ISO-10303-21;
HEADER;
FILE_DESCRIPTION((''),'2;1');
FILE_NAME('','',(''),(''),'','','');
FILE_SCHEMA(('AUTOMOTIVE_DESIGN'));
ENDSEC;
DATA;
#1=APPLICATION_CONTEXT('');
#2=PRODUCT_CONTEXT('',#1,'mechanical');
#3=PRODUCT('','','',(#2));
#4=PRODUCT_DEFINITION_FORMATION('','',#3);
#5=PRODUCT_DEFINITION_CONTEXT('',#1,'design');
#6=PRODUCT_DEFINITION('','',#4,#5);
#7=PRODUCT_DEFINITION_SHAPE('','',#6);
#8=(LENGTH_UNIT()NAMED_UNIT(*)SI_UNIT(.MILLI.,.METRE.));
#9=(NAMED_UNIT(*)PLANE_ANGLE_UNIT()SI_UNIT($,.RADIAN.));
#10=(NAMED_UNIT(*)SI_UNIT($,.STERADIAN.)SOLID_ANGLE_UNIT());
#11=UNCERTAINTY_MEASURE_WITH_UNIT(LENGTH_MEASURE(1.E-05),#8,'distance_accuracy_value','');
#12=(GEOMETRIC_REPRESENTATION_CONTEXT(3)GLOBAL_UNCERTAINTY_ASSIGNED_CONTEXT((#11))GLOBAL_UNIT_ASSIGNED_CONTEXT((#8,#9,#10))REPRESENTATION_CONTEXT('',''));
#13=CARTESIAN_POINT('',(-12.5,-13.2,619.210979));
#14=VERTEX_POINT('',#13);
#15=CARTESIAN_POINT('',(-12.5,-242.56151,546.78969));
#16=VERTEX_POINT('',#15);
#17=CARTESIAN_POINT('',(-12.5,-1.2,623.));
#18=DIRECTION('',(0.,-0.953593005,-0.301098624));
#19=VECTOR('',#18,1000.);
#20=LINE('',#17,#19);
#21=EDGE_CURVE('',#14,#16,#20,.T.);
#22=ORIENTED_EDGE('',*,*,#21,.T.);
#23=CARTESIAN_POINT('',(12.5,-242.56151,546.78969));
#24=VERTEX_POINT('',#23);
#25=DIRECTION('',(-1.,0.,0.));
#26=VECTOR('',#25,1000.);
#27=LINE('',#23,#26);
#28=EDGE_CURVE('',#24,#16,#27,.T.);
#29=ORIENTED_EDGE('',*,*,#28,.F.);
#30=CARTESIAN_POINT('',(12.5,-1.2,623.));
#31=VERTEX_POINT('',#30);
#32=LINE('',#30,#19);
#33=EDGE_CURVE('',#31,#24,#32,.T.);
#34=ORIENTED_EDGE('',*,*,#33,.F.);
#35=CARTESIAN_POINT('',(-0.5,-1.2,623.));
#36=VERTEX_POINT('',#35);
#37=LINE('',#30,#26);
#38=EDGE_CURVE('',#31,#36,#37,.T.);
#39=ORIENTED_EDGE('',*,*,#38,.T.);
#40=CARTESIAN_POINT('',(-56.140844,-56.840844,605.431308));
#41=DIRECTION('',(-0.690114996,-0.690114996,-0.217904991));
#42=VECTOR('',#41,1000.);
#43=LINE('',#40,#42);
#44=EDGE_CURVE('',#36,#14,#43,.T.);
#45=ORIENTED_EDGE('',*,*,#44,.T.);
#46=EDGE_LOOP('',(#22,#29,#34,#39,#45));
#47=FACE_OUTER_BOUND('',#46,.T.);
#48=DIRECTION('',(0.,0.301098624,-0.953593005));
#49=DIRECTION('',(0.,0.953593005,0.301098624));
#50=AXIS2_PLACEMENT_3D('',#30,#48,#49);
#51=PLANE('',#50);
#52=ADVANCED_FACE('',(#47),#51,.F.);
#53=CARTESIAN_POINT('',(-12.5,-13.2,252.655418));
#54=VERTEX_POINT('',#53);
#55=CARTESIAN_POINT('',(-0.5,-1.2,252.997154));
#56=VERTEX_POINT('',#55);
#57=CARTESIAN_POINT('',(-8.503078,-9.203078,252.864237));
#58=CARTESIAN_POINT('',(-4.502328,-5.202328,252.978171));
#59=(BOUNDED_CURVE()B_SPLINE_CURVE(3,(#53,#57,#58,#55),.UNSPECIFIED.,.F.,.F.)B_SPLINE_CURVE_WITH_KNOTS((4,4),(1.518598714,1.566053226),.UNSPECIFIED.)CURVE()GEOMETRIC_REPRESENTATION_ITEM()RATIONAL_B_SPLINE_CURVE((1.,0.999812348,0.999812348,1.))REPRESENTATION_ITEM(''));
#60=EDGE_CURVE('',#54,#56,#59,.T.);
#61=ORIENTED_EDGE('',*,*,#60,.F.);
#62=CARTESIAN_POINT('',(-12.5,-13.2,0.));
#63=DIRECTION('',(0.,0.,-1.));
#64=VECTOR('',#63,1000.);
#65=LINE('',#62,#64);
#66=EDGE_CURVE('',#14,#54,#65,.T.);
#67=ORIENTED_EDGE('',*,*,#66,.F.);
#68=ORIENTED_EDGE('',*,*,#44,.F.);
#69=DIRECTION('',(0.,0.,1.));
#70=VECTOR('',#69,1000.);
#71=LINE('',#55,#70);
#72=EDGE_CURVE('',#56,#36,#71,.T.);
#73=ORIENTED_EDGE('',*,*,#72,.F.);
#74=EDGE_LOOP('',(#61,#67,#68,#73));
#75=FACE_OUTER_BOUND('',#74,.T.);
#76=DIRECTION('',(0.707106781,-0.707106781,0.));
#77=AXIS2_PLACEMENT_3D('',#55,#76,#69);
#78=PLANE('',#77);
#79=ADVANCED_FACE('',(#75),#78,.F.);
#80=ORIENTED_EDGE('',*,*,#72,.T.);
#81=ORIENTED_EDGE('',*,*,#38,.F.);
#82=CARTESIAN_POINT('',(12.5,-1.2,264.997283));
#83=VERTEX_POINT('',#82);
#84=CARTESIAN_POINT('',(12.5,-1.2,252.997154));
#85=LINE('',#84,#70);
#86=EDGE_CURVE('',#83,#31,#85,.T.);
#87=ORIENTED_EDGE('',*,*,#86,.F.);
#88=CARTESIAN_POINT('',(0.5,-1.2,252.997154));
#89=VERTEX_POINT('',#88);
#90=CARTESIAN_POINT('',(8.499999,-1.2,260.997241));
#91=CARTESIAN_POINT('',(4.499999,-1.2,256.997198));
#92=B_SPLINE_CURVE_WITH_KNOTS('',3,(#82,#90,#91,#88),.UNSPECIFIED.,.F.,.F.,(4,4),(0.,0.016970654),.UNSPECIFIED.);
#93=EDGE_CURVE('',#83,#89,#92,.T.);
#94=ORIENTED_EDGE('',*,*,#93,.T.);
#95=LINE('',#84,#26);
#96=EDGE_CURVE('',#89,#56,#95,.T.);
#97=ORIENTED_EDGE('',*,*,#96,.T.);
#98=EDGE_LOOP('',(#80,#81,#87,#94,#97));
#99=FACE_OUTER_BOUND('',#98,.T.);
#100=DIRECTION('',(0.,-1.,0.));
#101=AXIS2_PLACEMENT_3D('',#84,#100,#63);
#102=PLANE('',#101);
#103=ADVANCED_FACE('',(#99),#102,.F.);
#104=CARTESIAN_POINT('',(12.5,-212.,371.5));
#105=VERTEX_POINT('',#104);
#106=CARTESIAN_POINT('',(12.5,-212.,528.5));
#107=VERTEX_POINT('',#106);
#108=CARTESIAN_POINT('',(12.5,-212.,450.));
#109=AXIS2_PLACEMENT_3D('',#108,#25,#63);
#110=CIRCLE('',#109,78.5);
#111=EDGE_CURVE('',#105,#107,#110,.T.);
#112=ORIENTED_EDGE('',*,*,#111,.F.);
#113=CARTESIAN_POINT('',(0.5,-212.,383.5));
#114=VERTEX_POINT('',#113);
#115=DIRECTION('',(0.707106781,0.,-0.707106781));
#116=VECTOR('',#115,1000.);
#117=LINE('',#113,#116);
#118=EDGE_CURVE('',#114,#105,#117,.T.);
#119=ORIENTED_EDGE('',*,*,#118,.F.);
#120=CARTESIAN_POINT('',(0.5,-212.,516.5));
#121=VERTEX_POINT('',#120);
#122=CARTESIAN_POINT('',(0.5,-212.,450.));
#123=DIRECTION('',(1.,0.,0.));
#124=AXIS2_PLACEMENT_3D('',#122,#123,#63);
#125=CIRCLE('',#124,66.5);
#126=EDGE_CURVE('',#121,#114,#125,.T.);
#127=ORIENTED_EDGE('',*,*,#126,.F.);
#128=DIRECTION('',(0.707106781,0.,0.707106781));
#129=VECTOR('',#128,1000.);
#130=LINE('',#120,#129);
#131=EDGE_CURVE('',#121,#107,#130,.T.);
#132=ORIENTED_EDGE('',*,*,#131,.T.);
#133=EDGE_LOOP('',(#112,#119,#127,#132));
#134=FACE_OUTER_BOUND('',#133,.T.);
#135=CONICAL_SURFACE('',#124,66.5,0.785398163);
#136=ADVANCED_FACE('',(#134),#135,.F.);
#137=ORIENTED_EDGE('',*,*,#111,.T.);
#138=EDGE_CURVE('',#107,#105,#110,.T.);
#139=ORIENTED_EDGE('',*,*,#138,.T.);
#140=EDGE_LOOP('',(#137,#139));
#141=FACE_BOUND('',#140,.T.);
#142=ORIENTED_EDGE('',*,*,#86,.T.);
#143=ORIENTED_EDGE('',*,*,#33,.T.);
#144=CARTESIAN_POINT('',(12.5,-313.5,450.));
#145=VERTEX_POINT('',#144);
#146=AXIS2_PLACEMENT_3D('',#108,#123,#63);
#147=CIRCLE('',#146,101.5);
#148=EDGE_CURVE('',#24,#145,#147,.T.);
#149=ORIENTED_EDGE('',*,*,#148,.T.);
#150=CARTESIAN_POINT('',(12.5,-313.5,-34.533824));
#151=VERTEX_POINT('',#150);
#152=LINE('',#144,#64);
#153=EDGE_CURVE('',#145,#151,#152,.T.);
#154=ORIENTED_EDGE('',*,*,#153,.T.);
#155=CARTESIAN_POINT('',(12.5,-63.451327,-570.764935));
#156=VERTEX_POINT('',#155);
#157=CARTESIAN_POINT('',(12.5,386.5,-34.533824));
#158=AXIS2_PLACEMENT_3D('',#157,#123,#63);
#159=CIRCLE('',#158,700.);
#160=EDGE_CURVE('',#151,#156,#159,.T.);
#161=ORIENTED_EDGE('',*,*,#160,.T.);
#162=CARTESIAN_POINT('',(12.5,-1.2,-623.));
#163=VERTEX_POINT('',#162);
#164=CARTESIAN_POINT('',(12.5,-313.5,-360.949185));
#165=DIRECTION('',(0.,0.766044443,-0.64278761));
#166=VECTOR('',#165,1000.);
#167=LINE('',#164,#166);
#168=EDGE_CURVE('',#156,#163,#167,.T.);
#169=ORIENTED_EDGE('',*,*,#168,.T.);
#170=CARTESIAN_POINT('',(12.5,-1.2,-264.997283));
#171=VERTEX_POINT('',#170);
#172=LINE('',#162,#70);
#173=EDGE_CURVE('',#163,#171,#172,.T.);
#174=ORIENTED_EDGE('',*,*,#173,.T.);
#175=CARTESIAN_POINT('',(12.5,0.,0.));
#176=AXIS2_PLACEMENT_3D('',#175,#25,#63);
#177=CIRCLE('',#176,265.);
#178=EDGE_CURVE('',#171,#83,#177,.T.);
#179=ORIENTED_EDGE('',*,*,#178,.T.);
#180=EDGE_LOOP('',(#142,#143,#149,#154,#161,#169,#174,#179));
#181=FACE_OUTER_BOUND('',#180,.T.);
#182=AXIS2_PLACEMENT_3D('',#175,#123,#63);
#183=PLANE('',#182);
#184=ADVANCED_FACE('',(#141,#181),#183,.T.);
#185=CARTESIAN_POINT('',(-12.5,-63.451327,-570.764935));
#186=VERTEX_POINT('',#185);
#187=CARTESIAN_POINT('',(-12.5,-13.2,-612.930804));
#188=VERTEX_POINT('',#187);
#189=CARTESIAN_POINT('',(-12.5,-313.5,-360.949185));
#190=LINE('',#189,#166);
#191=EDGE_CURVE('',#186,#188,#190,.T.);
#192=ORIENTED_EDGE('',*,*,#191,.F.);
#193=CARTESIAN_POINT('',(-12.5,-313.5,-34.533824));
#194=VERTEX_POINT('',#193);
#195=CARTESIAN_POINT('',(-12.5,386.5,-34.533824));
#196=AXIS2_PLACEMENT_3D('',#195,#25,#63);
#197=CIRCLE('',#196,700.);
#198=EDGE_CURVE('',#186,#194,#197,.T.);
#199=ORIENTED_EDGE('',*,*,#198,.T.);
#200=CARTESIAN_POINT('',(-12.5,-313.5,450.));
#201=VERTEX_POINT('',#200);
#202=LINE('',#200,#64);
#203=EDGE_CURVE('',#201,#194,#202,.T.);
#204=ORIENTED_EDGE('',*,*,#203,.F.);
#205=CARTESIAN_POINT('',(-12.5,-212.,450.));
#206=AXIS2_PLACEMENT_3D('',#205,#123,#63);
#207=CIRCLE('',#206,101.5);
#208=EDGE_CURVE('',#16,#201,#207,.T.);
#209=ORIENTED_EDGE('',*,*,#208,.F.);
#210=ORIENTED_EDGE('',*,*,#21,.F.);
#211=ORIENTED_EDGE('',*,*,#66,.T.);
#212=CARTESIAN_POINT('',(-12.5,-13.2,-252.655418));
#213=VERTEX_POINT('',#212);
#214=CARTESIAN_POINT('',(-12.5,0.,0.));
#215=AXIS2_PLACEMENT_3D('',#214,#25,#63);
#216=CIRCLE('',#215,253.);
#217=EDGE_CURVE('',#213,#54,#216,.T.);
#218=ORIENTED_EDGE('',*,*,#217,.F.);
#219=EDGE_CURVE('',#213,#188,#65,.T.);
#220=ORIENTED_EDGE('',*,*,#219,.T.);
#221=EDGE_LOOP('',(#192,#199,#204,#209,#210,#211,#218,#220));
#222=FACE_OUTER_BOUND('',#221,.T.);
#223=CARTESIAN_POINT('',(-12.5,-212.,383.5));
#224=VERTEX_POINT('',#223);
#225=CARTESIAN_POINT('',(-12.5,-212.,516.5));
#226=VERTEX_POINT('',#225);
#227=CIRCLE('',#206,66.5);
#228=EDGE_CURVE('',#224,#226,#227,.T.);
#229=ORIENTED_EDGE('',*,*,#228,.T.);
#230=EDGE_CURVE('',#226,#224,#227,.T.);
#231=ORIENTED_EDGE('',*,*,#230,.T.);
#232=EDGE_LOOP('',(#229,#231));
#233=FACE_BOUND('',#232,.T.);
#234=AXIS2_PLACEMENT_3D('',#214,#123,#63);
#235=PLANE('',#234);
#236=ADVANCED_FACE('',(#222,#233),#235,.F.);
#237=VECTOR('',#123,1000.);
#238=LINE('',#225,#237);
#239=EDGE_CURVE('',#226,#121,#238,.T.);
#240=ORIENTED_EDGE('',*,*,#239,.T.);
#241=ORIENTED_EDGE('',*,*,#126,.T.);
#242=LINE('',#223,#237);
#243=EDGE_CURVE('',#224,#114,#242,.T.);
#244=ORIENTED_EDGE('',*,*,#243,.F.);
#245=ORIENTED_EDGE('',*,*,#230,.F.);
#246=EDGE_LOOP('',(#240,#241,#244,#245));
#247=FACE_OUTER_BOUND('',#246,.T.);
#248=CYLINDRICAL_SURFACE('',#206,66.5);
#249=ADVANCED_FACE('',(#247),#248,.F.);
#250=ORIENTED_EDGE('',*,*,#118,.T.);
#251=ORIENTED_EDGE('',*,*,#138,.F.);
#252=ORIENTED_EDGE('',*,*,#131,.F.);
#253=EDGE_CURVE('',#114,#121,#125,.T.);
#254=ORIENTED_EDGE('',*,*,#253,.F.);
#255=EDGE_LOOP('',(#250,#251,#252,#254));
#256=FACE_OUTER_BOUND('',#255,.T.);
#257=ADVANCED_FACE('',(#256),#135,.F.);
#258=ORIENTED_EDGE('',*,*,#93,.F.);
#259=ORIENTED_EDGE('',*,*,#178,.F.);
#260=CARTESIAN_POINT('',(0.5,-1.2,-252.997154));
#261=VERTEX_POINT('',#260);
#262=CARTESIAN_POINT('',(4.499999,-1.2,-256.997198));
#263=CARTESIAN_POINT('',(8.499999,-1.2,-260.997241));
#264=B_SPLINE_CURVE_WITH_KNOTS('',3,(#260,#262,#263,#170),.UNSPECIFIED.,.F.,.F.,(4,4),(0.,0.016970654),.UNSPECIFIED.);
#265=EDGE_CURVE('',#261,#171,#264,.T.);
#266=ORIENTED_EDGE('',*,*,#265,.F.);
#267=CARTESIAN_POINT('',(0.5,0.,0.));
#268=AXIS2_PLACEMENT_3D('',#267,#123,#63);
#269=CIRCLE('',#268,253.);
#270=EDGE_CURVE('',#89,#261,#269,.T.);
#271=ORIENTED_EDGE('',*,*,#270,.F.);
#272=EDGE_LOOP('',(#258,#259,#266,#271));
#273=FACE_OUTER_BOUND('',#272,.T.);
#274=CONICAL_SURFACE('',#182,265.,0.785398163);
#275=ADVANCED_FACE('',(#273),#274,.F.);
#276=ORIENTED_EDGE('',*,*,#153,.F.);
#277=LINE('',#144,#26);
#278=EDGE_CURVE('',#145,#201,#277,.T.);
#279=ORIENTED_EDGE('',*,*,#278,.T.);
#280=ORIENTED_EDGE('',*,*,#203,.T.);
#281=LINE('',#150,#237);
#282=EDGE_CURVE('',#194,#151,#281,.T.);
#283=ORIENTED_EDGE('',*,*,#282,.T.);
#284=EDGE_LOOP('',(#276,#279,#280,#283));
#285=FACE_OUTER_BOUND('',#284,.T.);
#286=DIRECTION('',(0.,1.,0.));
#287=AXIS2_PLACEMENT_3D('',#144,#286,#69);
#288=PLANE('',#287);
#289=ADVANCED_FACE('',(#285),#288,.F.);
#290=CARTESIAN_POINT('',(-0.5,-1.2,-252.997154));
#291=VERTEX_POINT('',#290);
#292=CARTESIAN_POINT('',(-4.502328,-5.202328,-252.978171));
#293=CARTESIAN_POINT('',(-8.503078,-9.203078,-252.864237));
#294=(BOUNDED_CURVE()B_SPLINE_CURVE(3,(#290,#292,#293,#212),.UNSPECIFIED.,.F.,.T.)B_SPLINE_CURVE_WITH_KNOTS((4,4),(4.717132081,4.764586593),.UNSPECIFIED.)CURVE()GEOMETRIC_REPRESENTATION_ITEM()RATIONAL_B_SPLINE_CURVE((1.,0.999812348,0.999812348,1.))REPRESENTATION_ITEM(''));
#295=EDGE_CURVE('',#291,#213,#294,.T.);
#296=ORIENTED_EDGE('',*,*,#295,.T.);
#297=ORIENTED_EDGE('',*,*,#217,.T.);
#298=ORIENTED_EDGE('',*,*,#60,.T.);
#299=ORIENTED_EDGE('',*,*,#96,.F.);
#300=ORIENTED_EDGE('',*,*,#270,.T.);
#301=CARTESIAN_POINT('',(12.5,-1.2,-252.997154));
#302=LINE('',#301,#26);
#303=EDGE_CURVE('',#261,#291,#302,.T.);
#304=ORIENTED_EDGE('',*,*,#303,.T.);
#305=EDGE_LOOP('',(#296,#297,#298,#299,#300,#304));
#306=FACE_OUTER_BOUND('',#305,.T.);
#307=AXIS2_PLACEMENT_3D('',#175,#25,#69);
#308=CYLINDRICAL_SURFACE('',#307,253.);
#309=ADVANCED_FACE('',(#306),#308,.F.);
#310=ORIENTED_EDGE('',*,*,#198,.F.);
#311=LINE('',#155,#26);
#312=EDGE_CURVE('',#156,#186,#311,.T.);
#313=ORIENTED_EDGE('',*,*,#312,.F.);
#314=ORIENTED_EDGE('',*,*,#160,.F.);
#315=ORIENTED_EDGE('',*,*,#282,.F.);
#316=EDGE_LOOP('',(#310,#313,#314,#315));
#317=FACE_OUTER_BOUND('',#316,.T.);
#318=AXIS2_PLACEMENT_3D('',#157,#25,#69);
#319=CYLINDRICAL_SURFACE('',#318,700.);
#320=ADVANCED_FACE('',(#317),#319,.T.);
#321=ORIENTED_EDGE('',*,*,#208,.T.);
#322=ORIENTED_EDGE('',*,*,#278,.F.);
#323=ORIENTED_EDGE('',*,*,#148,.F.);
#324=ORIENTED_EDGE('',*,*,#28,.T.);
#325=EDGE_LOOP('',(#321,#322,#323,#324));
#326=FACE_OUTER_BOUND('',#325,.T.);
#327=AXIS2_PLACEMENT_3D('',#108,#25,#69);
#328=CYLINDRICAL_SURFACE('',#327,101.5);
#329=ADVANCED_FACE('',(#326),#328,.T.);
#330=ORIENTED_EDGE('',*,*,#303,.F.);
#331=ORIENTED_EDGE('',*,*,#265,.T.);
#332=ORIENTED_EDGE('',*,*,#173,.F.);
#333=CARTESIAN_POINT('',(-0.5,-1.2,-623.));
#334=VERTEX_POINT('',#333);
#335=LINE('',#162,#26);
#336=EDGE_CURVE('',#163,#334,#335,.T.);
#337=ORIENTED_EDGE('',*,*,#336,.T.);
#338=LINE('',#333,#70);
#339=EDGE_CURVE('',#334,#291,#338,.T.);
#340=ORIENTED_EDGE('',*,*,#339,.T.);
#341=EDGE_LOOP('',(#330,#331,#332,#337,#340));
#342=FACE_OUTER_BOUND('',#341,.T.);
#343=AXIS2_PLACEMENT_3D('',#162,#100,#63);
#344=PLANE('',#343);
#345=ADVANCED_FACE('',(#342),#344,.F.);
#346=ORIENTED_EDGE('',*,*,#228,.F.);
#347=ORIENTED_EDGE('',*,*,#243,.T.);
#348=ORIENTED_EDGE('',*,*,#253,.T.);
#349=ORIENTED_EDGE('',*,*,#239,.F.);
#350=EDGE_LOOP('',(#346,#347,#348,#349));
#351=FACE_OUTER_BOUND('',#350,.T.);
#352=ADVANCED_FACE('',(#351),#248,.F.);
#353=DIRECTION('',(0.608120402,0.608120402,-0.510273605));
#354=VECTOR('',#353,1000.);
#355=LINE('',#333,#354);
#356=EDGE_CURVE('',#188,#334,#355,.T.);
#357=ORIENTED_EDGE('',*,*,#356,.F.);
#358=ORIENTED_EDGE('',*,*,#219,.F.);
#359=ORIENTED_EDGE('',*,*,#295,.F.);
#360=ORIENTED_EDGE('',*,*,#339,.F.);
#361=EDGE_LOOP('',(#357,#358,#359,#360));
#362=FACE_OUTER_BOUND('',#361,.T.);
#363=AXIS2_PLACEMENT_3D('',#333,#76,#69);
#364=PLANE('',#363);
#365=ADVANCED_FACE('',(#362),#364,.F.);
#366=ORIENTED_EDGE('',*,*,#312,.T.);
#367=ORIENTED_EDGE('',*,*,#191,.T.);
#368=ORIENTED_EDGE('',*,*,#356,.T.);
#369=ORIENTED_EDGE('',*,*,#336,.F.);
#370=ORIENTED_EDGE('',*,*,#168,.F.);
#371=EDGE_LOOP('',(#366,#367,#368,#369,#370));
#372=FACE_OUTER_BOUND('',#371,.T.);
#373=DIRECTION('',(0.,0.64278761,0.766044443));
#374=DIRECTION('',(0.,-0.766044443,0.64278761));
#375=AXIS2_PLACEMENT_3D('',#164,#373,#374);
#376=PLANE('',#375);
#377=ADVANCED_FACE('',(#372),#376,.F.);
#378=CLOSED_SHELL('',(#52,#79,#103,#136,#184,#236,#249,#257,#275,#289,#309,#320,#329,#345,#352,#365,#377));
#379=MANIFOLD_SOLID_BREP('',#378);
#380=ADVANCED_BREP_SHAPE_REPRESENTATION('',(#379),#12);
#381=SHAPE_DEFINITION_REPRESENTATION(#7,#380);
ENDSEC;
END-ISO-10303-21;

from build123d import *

# Parameters (mm, degrees)
BOSS_EXTRUDE1_DEPTH     = 12.5
CUT_EXTRUDE1_DEPTH      = 698.543905428
CUT_EXTRUDE1_DEPTH_BACK = 698.543905428
SKETCH2_R               = 66.5
FILLET1_R               = 700
CHAMFER1_SIZE           = 12
CHAMFER2_SIZE           = 12


with BuildPart() as part:
    # Sketch1 → Boss-Extrude1 (new, symmetric)
    with BuildSketch(Plane(origin=(0, 0, 0), x_dir=(0, 0, -1), z_dir=(1, 0, 0))):
        with BuildLine():
            Line((623, -1.2), (252.997154134, -1.2))
            ThreePointArc((252.997154134, -1.2), (0, -253), (-252.997154134, -1.2))
            Line((-252.997154134, -1.2), (-623, -1.2))
            Line((-623, -1.2), (-546.789689993, -242.561510288))
            ThreePointArc((-546.789689993, -242.561510288), (-510.001069598, -293.866486715), (-450, -313.5))
            Line((-450, -313.5), (360.949185183, -313.5))
            Line((360.949185183, -313.5), (623, -1.2))
        make_face()
    extrude(amount=BOSS_EXTRUDE1_DEPTH, both=True)

    # Sketch2 → Cut-Extrude1 (cut, two sides: drawn at the far end of the back side and taken through both)
    with BuildSketch(Plane(origin=(0, 0, 0), x_dir=(0, 0, -1), z_dir=(1, 0, 0)).offset(-CUT_EXTRUDE1_DEPTH_BACK)):
        with Locations((-450, -212)):
            Circle(SKETCH2_R)
    extrude(amount=CUT_EXTRUDE1_DEPTH + CUT_EXTRUDE1_DEPTH_BACK, mode=Mode.SUBTRACT)

    # Fillet1
    fillet1_edges = [part.edges().sort_by_distance(p)[0] for p in [
        (0, -313.5, -360.949185183),
    ]]
    fillet(fillet1_edges, radius=FILLET1_R)

    # Chamfer1
    chamfer1_edges = [part.edges().sort_by_distance(p)[0] for p in [
        (12.5, -212, 516.5),
        (12.5, -253, 0),
    ]]
    chamfer(chamfer1_edges, length=CHAMFER1_SIZE)

    # Chamfer2
    chamfer2_edges = [part.edges().sort_by_distance(p)[0] for p in [
        (-12.5, -1.2, -437.998577067),
        (-12.5, -1.2, 437.998577067),
    ]]
    chamfer(chamfer2_edges, length=CHAMFER2_SIZE)


solid = part.part
